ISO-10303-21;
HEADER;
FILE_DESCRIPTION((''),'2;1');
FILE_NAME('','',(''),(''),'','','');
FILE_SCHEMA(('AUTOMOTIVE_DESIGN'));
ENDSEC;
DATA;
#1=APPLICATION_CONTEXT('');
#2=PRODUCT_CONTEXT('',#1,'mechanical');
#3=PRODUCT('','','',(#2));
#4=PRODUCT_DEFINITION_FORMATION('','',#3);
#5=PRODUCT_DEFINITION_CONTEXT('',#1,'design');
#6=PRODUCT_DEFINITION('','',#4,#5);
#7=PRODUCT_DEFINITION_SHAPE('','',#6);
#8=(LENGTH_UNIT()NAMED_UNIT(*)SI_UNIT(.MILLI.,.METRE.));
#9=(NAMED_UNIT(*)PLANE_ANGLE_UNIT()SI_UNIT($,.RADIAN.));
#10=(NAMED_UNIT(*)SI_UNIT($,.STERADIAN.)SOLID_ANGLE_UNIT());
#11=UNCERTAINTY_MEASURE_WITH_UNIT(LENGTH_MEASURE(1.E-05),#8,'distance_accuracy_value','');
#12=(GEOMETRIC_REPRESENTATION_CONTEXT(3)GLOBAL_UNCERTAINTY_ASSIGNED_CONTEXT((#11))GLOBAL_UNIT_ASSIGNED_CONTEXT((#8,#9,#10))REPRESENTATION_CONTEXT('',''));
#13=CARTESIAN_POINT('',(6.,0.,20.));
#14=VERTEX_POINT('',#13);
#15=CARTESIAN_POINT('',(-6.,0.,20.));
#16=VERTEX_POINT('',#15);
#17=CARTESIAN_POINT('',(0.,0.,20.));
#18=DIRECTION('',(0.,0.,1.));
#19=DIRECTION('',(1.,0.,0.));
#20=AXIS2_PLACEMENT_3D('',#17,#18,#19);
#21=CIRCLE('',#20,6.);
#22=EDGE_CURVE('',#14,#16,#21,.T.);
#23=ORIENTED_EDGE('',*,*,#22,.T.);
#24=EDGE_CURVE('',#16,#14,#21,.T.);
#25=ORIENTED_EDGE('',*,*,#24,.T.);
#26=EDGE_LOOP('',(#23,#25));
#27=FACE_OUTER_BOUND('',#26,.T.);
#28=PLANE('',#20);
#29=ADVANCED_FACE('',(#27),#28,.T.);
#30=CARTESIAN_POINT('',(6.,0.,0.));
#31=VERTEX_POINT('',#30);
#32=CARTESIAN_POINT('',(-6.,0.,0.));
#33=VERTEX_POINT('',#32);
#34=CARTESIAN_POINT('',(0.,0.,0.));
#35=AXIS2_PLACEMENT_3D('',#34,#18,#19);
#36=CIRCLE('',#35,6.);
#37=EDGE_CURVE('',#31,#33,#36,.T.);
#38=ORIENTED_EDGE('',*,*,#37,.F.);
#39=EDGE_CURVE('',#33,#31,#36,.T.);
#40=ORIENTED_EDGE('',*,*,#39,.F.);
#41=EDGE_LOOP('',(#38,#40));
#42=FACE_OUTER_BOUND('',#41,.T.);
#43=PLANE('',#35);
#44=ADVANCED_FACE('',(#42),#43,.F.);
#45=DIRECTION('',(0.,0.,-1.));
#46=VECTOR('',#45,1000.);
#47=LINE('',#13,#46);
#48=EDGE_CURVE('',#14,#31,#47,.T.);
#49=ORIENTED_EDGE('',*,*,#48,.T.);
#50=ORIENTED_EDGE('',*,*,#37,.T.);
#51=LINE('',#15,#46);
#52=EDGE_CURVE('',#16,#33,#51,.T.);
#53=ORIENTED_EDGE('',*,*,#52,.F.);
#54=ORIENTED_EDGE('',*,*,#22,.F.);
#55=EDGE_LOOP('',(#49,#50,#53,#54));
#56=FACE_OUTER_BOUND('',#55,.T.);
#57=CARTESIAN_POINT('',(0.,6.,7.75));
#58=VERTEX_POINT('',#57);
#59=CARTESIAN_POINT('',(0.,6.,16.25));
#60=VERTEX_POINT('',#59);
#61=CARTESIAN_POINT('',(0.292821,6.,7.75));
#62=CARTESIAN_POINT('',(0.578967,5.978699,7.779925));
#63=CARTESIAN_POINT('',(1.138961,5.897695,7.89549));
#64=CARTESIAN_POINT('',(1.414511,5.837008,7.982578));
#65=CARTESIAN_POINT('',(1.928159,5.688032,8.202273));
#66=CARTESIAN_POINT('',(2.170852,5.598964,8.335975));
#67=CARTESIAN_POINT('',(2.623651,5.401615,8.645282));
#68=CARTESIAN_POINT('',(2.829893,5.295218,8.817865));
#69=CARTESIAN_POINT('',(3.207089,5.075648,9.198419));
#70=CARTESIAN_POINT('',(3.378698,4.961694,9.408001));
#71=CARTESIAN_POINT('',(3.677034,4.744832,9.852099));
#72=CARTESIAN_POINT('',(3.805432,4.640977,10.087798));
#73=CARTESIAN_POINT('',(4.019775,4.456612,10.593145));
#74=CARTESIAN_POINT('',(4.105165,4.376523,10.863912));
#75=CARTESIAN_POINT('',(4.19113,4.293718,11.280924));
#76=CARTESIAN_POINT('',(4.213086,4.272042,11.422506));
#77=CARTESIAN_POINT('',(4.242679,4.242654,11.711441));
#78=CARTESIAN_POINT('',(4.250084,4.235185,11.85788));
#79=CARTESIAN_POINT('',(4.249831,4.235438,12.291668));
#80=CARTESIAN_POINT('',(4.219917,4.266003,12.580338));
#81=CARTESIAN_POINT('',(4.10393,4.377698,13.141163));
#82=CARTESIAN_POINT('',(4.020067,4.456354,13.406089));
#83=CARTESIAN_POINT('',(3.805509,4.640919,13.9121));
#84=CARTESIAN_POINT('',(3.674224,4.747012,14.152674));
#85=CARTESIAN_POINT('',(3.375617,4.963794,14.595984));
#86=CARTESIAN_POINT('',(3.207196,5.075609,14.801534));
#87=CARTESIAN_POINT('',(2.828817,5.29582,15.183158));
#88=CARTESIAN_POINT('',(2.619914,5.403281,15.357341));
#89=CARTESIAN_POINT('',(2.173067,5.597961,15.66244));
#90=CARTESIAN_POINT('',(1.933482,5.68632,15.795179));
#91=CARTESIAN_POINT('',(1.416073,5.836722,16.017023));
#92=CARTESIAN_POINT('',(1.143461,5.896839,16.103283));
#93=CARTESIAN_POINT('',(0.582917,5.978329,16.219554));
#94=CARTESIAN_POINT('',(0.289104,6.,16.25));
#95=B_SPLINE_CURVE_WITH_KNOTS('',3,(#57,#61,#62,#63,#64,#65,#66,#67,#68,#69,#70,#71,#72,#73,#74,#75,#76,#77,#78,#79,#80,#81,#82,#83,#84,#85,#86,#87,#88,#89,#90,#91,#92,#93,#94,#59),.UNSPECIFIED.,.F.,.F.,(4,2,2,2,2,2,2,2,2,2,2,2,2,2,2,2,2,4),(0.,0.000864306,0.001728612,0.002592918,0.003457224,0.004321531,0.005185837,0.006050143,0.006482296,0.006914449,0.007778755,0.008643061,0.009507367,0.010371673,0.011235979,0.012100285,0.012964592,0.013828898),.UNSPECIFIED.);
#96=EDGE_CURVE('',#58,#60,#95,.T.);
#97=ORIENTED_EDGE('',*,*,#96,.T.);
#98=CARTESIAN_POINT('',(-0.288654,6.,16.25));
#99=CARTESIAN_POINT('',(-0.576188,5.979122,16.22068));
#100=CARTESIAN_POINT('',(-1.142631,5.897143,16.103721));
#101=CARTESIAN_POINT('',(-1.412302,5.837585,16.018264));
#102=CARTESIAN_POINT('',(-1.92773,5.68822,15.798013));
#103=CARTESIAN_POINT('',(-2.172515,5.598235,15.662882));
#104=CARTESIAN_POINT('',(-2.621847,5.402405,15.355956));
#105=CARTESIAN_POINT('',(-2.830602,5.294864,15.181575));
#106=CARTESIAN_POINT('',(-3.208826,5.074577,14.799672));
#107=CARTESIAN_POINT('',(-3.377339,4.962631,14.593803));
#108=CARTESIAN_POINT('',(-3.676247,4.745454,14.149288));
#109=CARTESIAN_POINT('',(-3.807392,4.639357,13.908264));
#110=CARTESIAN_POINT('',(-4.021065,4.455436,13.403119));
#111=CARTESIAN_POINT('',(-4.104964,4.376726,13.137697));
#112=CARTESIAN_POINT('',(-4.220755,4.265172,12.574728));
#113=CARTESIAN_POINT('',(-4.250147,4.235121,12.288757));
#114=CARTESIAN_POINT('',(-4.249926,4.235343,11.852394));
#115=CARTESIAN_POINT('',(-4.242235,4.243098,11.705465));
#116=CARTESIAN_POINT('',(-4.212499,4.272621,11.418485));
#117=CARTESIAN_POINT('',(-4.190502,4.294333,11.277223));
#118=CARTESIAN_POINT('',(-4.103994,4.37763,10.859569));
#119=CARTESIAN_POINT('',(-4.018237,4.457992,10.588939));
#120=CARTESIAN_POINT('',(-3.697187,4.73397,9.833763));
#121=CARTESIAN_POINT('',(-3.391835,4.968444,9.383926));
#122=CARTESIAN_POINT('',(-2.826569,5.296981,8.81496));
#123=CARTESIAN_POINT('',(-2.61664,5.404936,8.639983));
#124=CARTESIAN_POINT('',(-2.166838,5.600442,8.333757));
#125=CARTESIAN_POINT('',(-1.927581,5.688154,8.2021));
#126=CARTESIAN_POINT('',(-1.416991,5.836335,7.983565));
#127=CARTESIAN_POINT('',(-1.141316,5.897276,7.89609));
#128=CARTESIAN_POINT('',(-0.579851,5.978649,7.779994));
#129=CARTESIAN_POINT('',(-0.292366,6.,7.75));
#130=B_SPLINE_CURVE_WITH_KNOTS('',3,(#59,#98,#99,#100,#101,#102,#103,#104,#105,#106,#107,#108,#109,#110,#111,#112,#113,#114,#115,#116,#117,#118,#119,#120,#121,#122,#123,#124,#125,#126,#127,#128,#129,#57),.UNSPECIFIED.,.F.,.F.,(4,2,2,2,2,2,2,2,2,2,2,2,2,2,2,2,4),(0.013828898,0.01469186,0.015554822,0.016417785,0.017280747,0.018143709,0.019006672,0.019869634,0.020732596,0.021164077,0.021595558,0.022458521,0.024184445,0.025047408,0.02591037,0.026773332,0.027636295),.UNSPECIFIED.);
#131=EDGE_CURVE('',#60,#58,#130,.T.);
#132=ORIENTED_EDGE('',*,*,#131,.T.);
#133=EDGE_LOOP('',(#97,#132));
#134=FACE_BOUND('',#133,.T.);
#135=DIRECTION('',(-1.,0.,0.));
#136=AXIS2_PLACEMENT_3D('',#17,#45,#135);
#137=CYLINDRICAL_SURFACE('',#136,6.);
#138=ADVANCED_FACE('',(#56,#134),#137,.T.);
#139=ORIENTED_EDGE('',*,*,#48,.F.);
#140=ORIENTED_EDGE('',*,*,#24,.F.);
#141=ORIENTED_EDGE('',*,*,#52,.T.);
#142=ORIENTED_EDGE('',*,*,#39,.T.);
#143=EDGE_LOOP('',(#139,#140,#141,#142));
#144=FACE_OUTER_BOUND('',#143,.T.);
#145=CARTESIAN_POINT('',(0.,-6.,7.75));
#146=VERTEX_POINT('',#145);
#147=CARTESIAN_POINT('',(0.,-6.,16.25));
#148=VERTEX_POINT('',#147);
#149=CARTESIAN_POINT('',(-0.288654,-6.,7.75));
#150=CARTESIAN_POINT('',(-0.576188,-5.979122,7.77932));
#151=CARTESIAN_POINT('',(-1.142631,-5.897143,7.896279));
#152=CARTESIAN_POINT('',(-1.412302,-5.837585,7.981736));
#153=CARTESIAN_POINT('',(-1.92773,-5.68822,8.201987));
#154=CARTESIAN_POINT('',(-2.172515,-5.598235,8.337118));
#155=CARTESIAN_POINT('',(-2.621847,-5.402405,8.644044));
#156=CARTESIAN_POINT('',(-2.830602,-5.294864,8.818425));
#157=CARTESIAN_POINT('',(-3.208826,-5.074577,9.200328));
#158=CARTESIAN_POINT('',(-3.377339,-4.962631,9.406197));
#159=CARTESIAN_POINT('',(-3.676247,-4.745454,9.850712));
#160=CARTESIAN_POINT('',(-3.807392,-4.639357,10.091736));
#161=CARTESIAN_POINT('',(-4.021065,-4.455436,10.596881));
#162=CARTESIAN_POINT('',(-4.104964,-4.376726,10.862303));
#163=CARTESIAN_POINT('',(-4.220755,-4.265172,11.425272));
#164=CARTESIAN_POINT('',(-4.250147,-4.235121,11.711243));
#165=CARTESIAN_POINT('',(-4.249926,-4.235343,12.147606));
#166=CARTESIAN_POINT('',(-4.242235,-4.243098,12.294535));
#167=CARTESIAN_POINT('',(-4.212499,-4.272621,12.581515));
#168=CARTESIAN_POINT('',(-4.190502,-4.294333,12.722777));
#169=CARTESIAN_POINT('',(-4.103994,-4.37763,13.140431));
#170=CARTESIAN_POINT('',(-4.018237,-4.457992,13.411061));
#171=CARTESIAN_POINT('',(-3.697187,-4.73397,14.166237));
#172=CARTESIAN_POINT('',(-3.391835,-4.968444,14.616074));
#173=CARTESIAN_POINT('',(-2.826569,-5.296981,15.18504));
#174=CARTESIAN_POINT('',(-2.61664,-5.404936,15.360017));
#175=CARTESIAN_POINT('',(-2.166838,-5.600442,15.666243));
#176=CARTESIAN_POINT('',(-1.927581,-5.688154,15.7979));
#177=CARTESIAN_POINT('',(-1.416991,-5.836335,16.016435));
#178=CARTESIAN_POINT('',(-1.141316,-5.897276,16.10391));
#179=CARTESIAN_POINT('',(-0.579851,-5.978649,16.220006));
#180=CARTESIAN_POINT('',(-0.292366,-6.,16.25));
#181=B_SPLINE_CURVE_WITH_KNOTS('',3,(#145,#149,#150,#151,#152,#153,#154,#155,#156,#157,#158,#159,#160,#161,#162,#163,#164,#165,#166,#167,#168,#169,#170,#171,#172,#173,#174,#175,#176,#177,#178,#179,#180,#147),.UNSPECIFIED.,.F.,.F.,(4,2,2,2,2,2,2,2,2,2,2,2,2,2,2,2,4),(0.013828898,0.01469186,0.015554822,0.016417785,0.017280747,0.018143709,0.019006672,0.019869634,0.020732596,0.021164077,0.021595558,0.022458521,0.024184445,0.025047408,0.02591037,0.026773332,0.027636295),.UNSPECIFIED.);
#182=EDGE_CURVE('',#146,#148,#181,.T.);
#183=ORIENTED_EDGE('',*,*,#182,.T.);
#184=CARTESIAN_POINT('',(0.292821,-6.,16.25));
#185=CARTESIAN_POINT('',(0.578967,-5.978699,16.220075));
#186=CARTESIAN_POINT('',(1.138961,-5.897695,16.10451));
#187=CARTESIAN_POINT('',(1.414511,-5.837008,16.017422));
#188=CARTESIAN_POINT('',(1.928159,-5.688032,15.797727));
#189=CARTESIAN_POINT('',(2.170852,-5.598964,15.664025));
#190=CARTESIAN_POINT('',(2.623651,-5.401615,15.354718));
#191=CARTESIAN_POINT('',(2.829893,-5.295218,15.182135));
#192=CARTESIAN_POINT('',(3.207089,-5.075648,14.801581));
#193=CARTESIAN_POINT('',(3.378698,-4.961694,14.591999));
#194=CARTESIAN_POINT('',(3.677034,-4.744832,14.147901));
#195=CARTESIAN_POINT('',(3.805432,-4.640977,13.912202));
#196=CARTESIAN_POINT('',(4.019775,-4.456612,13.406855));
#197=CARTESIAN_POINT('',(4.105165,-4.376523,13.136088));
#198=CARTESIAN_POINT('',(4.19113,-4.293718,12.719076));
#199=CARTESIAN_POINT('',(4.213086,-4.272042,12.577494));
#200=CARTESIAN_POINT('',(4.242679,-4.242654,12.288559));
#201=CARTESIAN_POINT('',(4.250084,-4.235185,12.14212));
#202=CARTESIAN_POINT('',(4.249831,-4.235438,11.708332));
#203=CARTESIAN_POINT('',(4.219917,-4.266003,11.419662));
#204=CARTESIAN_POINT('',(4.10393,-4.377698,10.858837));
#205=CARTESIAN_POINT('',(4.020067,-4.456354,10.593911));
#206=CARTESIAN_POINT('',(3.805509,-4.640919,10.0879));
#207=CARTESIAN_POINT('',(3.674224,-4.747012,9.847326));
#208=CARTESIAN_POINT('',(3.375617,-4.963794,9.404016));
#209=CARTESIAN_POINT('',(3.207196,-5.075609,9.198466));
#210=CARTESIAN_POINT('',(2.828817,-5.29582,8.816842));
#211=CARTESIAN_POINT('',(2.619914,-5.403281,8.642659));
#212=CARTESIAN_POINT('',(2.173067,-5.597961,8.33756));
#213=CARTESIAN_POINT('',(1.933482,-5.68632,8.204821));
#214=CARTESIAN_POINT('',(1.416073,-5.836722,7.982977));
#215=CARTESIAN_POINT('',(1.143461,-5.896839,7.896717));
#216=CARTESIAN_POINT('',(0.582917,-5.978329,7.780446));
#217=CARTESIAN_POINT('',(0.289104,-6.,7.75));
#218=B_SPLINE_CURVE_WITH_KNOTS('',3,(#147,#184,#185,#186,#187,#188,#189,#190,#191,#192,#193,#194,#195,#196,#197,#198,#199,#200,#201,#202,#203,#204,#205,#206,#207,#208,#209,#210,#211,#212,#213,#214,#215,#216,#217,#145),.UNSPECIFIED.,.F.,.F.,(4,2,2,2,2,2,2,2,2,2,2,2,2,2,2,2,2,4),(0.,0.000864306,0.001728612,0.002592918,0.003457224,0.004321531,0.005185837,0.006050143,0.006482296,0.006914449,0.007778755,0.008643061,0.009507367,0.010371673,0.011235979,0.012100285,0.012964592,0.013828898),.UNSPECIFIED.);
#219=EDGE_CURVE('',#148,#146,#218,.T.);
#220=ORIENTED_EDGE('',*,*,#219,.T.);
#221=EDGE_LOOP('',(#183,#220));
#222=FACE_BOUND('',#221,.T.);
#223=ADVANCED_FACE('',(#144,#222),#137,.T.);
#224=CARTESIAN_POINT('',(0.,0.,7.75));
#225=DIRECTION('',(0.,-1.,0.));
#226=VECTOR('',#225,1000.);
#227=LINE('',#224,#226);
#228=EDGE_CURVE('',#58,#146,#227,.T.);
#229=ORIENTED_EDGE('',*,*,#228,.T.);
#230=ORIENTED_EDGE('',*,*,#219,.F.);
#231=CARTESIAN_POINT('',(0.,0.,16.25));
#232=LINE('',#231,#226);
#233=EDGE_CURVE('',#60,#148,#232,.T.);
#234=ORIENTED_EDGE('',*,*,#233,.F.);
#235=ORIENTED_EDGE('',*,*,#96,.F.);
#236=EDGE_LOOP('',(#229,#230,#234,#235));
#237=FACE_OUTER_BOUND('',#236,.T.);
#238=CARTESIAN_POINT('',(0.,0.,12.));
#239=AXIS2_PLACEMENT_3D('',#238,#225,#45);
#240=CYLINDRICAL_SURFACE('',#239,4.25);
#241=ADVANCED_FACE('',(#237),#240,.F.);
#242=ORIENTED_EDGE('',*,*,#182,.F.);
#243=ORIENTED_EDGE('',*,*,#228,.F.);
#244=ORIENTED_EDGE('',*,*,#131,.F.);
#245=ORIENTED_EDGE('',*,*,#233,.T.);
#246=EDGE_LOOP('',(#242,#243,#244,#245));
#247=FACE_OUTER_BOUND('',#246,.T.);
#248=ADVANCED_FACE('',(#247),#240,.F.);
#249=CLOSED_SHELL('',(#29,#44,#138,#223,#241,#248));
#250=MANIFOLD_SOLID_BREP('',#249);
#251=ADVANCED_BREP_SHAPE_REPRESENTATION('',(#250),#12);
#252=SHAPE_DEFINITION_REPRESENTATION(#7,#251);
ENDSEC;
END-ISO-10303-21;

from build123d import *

# Parameters (mm, degrees)
SKETCH1_R              = 6
BOSS_EXTRUDE1_DEPTH    = 20
SKETCH5_W              = 4.25
SKETCH5_H              = 6
M10_TAPPED_HOLE1_D     = 8.5
M10_TAPPED_HOLE1_DEPTH = 27.5
M10_TAPPED_HOLE1_TIP   = 2.553657631


with BuildPart() as part:
    # Sketch1 → Boss-Extrude1 (new body)
    with BuildSketch(Plane.XY):
        Circle(SKETCH1_R)
    extrude(amount=BOSS_EXTRUDE1_DEPTH)

    # Sketch5 → M10 Tapped Hole2 (revolve, cut)
    with BuildSketch(Plane(origin=(0, 0, 12), x_dir=(0, 0, -1), z_dir=(1, 0, 0))):
        with Locations((2.125, 3)):
            Rectangle(SKETCH5_W, SKETCH5_H)
    revolve(axis=Axis((0, -6.35, 12), (0, 1, 0)), mode=Mode.SUBTRACT)

    # M10 Tapped Hole1
    with Locations(Plane(origin=(0, 0, 0), x_dir=(1, 0, 0), z_dir=(0, 1, 0))):
        with Locations((0, -12)):
            Hole(M10_TAPPED_HOLE1_D / 2, depth=M10_TAPPED_HOLE1_DEPTH)
            with Locations((0, 0, -(M10_TAPPED_HOLE1_DEPTH + M10_TAPPED_HOLE1_TIP / 2))):  # 118° drill point
                Cone(0, M10_TAPPED_HOLE1_D / 2, M10_TAPPED_HOLE1_TIP, mode=Mode.SUBTRACT)


solid = part.part
